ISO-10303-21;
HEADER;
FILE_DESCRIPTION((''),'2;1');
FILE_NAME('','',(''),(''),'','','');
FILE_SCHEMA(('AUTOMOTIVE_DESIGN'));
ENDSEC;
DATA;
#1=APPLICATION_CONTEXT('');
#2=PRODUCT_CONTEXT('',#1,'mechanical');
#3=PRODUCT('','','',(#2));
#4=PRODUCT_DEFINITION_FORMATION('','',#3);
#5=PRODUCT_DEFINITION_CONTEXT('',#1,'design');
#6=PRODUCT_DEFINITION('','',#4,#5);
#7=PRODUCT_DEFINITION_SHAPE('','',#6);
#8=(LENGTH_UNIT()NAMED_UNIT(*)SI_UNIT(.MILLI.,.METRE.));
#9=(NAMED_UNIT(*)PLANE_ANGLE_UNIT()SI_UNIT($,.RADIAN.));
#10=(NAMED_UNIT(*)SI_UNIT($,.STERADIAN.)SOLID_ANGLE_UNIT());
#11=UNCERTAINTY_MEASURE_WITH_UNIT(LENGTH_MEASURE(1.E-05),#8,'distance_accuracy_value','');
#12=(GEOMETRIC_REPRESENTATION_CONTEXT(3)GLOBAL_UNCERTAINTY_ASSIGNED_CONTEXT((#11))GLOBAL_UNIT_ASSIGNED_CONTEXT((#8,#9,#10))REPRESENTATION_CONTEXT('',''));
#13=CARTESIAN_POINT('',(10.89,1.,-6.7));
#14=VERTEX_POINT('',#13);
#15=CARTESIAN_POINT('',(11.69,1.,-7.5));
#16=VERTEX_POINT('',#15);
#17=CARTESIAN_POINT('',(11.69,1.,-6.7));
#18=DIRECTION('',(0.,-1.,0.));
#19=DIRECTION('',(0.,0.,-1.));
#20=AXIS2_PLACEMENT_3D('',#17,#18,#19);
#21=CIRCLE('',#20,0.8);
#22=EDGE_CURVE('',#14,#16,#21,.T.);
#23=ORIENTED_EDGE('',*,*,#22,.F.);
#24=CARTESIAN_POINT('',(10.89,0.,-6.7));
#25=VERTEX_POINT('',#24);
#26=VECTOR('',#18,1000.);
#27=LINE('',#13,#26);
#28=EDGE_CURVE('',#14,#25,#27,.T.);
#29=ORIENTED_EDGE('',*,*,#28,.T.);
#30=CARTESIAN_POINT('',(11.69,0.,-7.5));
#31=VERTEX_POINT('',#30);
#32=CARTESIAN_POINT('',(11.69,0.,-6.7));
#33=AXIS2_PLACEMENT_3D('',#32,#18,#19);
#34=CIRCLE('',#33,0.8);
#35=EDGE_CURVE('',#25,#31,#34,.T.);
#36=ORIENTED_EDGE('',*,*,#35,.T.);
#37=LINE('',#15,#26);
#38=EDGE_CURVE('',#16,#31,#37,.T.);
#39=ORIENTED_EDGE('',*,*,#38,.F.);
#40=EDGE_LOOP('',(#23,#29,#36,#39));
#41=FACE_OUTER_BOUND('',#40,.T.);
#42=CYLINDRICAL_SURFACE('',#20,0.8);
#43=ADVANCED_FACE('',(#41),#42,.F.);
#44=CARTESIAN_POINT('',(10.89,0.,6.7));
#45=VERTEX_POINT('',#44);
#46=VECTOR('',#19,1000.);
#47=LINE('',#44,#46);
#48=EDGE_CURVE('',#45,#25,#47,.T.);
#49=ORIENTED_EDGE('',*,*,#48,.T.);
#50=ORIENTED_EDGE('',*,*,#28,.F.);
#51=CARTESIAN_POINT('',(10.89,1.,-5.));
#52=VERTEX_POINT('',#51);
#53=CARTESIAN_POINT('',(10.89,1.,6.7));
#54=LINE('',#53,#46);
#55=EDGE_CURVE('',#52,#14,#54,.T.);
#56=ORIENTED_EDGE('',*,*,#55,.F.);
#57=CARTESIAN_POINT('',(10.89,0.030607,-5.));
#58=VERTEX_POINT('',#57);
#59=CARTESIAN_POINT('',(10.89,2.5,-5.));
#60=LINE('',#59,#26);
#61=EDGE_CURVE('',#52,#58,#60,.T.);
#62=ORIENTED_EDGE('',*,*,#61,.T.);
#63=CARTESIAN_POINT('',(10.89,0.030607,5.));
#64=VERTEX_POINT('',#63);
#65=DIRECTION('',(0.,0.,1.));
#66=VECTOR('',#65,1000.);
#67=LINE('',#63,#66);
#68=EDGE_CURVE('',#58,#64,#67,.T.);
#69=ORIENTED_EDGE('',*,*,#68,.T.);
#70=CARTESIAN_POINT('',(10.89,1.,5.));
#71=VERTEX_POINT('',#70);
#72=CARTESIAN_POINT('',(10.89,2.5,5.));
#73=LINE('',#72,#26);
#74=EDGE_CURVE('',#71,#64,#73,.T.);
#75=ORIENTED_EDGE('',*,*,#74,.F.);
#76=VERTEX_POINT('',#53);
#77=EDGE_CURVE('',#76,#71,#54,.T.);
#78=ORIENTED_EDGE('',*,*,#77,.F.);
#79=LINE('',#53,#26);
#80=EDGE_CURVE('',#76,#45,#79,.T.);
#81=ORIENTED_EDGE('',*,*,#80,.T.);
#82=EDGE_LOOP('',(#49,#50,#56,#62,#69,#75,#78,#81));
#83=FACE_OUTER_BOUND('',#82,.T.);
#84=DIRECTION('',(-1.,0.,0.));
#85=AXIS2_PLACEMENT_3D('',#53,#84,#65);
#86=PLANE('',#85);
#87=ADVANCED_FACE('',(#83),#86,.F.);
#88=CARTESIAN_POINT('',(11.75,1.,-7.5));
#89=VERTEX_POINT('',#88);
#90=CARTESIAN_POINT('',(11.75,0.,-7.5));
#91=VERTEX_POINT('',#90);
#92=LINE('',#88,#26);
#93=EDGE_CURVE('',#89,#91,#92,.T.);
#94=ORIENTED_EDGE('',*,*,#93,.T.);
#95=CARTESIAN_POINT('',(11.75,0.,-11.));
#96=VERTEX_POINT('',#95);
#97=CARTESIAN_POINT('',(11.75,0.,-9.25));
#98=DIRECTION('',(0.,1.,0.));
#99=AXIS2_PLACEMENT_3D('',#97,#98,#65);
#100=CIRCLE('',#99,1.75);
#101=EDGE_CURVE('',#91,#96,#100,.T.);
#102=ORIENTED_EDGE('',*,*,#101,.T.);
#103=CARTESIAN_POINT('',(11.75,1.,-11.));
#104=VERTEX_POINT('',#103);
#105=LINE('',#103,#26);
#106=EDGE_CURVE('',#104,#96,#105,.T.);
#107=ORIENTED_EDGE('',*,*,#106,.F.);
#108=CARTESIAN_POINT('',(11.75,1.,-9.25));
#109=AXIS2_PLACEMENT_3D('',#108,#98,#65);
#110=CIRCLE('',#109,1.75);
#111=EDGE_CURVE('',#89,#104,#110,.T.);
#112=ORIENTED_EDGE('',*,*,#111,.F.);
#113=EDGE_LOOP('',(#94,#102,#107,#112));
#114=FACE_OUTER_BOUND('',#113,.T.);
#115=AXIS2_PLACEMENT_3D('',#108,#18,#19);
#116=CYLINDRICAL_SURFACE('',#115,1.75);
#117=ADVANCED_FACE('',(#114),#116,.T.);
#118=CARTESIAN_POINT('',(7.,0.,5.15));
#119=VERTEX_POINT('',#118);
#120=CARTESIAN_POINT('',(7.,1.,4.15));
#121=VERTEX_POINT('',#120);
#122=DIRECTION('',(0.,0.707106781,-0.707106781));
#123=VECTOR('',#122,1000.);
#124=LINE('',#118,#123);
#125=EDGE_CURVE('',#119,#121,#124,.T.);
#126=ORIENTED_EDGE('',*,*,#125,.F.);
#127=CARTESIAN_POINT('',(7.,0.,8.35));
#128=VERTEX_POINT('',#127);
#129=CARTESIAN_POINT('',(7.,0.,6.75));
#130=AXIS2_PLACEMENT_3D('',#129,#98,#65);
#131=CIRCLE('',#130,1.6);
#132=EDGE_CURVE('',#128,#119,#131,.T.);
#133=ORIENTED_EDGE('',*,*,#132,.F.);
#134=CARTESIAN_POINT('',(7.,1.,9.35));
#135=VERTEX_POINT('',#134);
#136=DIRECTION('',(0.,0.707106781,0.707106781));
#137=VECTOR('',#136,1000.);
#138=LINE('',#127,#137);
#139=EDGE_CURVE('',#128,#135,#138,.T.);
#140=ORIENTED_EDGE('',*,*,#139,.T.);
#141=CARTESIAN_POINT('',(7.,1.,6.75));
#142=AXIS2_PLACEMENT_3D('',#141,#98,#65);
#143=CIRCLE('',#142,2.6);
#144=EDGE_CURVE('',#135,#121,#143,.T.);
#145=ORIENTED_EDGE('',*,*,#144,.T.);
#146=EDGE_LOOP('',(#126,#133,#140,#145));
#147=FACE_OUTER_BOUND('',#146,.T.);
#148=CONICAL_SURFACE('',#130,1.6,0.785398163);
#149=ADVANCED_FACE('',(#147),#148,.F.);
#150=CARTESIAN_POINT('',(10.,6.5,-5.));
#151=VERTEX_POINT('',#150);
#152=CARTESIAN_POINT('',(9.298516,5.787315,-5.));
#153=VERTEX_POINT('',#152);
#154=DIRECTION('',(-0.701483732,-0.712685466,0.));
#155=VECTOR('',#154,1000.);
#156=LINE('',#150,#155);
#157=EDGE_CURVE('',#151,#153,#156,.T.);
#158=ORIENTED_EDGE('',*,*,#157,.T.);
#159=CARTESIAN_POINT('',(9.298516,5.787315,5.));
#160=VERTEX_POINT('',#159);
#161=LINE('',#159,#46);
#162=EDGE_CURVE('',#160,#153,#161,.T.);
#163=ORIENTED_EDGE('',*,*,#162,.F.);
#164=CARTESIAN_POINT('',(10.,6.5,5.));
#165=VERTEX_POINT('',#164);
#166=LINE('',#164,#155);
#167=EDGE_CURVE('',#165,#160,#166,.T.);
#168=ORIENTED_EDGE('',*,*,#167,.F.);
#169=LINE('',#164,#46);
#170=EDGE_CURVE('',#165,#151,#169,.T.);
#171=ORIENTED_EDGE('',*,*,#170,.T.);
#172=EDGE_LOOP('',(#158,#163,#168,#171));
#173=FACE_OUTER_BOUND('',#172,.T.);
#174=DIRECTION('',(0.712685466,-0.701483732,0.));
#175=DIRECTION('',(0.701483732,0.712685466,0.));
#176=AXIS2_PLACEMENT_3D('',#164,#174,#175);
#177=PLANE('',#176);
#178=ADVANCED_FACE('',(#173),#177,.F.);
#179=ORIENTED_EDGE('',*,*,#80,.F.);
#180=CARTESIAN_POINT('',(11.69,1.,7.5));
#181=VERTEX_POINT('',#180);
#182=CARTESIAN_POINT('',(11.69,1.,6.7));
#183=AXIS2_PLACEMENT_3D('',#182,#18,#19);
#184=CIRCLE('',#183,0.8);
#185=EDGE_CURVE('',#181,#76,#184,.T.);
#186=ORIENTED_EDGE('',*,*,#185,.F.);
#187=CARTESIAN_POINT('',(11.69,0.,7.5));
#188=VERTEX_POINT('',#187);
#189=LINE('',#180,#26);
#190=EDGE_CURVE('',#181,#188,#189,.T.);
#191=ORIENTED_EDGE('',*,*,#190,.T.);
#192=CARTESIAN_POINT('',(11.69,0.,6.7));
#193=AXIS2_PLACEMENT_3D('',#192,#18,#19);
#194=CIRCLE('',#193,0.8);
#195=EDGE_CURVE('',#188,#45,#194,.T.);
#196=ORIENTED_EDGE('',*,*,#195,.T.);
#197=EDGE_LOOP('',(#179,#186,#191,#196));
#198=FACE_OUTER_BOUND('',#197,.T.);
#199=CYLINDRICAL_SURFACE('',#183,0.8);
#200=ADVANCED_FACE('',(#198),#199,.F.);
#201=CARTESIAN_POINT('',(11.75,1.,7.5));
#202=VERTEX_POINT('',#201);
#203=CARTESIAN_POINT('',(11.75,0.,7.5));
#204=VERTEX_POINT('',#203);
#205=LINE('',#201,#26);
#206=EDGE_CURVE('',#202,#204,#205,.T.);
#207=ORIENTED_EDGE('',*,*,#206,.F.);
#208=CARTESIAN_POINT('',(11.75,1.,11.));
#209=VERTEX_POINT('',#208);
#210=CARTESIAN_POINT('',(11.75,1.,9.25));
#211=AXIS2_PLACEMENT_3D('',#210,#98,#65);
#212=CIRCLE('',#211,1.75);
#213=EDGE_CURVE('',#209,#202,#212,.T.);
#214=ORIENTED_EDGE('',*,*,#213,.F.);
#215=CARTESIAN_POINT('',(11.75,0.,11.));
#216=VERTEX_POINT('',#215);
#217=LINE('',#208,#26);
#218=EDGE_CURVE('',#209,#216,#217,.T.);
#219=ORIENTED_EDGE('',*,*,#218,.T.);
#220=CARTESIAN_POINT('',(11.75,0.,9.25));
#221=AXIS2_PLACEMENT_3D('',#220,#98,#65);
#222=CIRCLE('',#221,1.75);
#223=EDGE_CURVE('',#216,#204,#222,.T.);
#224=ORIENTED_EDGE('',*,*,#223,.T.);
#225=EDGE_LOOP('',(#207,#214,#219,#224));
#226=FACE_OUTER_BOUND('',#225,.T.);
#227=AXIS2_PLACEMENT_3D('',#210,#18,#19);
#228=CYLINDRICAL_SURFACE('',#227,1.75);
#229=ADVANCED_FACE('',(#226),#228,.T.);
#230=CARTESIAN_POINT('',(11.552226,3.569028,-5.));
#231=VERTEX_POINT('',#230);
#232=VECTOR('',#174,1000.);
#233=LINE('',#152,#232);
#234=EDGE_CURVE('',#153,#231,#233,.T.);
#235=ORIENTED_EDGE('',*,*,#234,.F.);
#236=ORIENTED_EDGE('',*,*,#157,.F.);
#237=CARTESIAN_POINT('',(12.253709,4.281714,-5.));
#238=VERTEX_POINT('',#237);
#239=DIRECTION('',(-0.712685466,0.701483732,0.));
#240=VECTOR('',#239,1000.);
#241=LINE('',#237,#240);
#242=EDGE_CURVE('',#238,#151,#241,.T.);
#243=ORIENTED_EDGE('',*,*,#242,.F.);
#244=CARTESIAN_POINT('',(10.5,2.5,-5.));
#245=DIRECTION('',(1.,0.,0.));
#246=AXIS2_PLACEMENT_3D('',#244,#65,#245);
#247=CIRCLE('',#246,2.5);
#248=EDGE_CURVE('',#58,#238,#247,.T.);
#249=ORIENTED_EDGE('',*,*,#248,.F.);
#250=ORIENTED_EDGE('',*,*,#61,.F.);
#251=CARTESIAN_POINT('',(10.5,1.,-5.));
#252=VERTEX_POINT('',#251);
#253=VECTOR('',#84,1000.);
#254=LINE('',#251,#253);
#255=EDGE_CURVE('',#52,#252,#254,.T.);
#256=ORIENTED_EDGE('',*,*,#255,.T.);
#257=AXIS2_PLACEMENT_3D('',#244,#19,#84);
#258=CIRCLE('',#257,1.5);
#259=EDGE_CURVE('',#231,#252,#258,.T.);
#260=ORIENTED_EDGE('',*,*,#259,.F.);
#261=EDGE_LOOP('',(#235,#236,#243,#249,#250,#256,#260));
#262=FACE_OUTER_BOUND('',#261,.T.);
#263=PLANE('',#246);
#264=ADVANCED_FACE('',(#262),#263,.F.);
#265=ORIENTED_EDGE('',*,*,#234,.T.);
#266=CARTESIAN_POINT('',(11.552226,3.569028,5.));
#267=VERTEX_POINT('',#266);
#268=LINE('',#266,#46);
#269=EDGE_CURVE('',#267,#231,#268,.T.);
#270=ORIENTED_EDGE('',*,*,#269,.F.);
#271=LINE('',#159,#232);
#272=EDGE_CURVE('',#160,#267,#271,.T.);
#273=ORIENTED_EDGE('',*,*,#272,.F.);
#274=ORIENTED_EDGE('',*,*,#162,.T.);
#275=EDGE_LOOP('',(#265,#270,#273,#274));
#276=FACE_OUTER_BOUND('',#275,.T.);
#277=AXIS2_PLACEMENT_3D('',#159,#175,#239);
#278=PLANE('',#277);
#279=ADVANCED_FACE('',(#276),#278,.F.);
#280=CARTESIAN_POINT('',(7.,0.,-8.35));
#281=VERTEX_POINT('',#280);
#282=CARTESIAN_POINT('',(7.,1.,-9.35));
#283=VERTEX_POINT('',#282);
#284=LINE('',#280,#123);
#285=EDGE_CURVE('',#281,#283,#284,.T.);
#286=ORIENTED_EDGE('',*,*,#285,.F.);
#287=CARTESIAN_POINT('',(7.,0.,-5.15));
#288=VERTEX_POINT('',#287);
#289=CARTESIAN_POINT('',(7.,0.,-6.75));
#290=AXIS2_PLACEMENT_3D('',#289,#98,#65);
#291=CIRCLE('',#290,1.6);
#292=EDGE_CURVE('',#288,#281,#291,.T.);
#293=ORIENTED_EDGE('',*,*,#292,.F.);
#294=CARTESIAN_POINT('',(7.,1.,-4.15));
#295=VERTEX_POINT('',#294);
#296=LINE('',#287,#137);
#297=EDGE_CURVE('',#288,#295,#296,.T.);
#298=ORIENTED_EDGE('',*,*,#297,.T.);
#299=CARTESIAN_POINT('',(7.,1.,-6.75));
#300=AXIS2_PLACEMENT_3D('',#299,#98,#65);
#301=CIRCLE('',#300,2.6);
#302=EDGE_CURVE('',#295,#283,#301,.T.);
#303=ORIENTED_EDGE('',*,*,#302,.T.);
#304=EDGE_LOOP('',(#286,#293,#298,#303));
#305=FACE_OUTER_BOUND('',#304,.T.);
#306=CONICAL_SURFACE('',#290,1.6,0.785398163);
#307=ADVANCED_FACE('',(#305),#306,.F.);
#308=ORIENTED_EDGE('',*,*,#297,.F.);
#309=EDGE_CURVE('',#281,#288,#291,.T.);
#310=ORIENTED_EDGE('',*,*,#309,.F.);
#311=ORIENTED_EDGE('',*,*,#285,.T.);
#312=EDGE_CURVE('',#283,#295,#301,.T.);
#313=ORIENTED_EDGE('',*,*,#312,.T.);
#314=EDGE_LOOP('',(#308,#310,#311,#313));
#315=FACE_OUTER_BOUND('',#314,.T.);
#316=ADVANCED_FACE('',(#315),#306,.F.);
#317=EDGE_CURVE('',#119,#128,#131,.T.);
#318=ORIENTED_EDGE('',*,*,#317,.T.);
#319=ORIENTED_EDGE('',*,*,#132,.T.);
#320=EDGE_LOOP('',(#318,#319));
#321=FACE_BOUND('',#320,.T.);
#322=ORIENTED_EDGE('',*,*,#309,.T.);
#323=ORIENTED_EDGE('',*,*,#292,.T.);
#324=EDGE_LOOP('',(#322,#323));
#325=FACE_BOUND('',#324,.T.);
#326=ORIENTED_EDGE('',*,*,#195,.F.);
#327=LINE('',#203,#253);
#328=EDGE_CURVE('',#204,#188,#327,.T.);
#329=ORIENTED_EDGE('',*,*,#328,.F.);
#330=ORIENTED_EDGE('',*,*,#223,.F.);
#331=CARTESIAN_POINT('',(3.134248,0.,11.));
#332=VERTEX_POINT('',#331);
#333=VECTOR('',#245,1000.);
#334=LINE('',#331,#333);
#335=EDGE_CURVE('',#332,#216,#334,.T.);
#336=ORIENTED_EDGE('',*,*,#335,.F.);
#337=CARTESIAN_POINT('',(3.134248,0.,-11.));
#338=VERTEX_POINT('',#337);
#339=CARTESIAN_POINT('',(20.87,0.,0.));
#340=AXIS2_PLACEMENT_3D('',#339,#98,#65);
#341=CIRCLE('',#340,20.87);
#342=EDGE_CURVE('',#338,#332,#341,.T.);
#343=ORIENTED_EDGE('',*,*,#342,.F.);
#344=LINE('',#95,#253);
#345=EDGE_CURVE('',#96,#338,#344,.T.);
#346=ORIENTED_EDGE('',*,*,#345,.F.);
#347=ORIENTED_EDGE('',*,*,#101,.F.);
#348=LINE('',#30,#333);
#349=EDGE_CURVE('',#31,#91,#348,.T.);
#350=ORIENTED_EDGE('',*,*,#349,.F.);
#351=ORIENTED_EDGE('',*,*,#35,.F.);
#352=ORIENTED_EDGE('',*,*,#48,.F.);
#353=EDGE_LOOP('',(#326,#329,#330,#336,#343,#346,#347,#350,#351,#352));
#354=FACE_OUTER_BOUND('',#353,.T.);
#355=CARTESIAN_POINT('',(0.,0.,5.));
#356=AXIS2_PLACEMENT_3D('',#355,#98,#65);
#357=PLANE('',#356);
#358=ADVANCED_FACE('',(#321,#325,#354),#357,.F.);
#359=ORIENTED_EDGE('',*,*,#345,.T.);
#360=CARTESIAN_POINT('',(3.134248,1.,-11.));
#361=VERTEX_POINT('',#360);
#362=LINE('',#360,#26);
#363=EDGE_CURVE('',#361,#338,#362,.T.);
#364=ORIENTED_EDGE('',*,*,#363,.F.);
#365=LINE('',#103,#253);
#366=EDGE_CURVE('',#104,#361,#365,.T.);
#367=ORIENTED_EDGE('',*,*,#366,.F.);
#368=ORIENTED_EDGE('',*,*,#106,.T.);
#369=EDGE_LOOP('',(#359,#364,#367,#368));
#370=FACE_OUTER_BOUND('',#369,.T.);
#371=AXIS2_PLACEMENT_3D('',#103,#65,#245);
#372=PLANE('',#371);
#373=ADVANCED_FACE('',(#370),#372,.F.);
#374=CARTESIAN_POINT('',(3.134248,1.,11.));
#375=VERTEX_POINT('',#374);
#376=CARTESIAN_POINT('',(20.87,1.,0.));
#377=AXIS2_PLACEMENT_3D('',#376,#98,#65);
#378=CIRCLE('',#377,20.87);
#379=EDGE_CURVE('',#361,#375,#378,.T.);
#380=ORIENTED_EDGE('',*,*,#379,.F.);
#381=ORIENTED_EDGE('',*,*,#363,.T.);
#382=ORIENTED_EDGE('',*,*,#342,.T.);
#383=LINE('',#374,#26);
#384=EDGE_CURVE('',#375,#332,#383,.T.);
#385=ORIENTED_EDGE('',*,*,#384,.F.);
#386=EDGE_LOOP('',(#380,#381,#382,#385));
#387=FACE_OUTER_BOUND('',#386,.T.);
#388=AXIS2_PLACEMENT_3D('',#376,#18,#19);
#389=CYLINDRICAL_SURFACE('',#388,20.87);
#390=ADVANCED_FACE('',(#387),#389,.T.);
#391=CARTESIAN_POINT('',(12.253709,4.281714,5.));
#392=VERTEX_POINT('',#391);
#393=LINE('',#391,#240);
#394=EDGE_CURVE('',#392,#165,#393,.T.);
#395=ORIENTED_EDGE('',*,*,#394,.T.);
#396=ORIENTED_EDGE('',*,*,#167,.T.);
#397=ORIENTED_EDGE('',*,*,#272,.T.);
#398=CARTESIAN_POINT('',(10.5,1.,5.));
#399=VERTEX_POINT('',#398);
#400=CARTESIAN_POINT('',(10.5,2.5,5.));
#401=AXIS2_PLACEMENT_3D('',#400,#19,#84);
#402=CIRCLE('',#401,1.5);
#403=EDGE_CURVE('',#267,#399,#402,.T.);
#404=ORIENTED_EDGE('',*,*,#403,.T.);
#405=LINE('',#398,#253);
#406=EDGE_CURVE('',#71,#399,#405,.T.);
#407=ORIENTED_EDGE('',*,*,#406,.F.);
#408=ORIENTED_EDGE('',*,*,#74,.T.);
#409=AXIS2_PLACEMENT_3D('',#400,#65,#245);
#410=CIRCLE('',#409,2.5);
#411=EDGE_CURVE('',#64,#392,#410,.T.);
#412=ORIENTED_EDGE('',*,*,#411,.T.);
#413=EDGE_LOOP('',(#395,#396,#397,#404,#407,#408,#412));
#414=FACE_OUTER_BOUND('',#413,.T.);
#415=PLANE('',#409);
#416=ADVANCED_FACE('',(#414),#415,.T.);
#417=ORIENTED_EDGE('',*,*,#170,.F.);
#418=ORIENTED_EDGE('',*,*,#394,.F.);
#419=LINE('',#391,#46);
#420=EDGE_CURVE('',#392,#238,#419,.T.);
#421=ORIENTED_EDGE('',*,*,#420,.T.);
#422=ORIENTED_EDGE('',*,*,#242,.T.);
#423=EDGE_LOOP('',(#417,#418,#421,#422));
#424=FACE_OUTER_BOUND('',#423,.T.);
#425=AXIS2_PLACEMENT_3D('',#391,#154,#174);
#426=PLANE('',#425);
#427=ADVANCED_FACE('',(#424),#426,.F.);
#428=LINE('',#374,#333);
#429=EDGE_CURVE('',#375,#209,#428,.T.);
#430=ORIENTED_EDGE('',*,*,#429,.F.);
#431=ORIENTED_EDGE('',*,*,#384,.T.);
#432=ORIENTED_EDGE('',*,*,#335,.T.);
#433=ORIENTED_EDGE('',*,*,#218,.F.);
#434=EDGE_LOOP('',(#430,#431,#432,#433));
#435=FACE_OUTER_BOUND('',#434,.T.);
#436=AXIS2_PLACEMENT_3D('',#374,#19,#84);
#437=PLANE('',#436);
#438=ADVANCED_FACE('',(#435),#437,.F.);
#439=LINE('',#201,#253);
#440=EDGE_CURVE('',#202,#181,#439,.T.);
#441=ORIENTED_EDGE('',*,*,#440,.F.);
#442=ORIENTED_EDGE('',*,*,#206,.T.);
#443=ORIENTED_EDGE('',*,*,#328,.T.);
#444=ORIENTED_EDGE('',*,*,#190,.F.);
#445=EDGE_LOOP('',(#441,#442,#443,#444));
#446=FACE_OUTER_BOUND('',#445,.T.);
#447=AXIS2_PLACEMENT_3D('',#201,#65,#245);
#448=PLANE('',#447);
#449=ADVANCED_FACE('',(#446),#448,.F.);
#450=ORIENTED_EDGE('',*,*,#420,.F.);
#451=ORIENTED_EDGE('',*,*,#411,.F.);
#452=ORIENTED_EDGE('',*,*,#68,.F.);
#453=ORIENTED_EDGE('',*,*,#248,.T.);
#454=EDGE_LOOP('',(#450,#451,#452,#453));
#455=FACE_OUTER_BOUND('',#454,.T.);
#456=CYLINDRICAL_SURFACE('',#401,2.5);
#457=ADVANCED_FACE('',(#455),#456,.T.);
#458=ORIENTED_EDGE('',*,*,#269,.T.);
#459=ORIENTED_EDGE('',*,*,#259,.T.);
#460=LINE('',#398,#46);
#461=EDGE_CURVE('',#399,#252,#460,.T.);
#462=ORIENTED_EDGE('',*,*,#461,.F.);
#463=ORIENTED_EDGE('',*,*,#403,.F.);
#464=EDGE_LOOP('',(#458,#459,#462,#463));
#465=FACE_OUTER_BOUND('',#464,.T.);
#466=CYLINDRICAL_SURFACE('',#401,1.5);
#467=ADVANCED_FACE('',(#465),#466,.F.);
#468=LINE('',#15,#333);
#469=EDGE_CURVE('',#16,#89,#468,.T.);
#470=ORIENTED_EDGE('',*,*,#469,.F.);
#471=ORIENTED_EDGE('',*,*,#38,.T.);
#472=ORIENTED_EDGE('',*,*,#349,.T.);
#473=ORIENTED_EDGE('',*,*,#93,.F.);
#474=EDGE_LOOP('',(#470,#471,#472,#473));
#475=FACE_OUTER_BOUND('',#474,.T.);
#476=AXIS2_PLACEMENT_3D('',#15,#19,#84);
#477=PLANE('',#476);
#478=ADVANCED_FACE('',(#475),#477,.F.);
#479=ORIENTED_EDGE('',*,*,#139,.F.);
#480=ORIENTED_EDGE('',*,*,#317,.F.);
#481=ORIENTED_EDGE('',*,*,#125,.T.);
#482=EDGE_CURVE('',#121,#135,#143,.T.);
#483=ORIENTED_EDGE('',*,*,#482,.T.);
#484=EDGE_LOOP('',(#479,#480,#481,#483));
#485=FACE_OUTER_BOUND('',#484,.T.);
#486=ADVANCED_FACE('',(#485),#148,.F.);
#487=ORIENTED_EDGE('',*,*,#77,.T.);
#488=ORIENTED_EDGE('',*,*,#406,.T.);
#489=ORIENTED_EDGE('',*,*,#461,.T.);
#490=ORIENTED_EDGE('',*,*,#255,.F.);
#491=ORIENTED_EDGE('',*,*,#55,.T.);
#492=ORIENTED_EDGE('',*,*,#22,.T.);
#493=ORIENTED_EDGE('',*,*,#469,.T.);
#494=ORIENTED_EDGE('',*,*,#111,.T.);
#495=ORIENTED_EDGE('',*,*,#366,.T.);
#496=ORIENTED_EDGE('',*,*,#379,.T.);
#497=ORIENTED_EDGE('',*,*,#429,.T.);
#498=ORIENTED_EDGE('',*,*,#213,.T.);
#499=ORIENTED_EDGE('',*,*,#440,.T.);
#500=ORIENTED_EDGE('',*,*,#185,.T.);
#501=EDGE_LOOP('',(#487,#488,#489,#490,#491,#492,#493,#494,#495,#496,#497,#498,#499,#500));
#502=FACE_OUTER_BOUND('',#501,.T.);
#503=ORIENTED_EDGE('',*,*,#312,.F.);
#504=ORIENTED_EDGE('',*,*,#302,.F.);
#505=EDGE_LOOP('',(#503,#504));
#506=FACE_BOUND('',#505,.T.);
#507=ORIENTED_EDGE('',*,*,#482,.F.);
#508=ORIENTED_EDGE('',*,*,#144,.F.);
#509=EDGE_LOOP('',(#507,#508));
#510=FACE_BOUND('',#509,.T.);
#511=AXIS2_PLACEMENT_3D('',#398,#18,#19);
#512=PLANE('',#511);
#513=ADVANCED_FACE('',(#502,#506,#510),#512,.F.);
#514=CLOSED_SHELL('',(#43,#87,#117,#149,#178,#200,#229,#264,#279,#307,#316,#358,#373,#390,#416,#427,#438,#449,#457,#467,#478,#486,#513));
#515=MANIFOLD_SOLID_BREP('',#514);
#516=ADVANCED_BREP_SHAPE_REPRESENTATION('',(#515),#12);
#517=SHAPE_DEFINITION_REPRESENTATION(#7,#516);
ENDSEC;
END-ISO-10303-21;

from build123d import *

# Parameters (mm, degrees)
EXTRUDE_1_DEPTH      = 5
EXTRUDE_1_DEPTH_BACK = 5
EXTRUDE_2_DEPTH      = 1
SKETCH_3_W           = 100
SKETCH_3_H           = 100
SKETCH_3_R           = 20.87
CUT_EXTRUDE_1_DEPTH  = 2


with BuildPart() as part:
    # 草图1 → 凸台-拉伸1 (new, two sides: drawn at the far end of the back side and taken through both)
    with BuildSketch(Plane.XY.offset(-EXTRUDE_1_DEPTH_BACK)):
        with BuildLine():
            Line((0, 0), (10.5, 0))
            ThreePointArc((10.5, 0), (12.813469706, 1.552446351), (12.253709329, 4.281713666))
            Line((12.253709329, 4.281713666), (10, 6.5))
            Line((10, 6.5), (9.298516268, 5.787314534))
            Line((9.298516268, 5.787314534), (11.552225598, 3.5690282))
            ThreePointArc((11.552225598, 3.5690282), (11.888081824, 1.931467811), (10.5, 1))
            Line((10.5, 1), (0, 1))
            Line((0, 1), (0, 0))
        make_face()
    extrude(amount=EXTRUDE_1_DEPTH + EXTRUDE_1_DEPTH_BACK)

    # 草图2 → 凸台-拉伸2 (add)
    with BuildSketch(Plane(origin=(0, 0, 0), x_dir=(1, 0, 0), z_dir=(0, 1, 0))):
        with BuildLine():
            Line((3.134247972, -11), (11.75, -11))
            ThreePointArc((11.75, -11), (13.5, -9.25), (11.75, -7.5))
            Line((11.75, -7.5), (11.69, -7.5))
            ThreePointArc((11.69, -7.5), (11.124314575, -7.265685425), (10.89, -6.7))
            Line((10.89, -6.7), (10.89, 6.7))
            ThreePointArc((10.89, 6.7), (11.124314575, 7.265685425), (11.69, 7.5))
            Line((11.69, 7.5), (11.75, 7.5))
            ThreePointArc((11.75, 7.5), (13.5, 9.25), (11.75, 11))
            Line((11.75, 11), (3.134247972, 11))
            ThreePointArc((3.134247972, 11), (0, 0), (3.134247972, -11))
        make_face()
    extrude(amount=EXTRUDE_2_DEPTH)

    # 草图3 → 切除-拉伸1 (cut)
    with BuildSketch(Plane(origin=(0, 0, 0), x_dir=(1, 0, 0), z_dir=(0, 1, 0))):
        Rectangle(SKETCH_3_W, SKETCH_3_H)
        with Locations((20.87, 0)):
            Circle(SKETCH_3_R, mode=Mode.SUBTRACT)
    extrude(amount=CUT_EXTRUDE_1_DEPTH, mode=Mode.SUBTRACT)

    # 草图4 → 切除-旋转1 (revolve, cut)
    with BuildSketch(Plane.XY.offset(6.75), mode=Mode.PRIVATE) as cut_revolve_1_sk:
        Polygon((7, 1), (9.6, 1), (8.6, 0), (7, 0), align=None)
    revolve(cut_revolve_1_sk.sketch.rotate(Axis((7, 0, 6.75), (0, 1, 0)), 270), axis=Axis((7, 0, 6.75), (0, 1, 0)), mode=Mode.SUBTRACT)

    # 草图5 → 切除-旋转2 (revolve, cut)
    with BuildSketch(Plane.XY.offset(-6.75), mode=Mode.PRIVATE) as cut_revolve_2_sk:
        Polygon((7, 1), (9.6, 1), (8.6, 0), (7, 0), align=None)
    revolve(cut_revolve_2_sk.sketch.rotate(Axis((7, 0, -6.75), (0, 1, 0)), 270), axis=Axis((7, 0, -6.75), (0, 1, 0)), mode=Mode.SUBTRACT)


solid = part.part
